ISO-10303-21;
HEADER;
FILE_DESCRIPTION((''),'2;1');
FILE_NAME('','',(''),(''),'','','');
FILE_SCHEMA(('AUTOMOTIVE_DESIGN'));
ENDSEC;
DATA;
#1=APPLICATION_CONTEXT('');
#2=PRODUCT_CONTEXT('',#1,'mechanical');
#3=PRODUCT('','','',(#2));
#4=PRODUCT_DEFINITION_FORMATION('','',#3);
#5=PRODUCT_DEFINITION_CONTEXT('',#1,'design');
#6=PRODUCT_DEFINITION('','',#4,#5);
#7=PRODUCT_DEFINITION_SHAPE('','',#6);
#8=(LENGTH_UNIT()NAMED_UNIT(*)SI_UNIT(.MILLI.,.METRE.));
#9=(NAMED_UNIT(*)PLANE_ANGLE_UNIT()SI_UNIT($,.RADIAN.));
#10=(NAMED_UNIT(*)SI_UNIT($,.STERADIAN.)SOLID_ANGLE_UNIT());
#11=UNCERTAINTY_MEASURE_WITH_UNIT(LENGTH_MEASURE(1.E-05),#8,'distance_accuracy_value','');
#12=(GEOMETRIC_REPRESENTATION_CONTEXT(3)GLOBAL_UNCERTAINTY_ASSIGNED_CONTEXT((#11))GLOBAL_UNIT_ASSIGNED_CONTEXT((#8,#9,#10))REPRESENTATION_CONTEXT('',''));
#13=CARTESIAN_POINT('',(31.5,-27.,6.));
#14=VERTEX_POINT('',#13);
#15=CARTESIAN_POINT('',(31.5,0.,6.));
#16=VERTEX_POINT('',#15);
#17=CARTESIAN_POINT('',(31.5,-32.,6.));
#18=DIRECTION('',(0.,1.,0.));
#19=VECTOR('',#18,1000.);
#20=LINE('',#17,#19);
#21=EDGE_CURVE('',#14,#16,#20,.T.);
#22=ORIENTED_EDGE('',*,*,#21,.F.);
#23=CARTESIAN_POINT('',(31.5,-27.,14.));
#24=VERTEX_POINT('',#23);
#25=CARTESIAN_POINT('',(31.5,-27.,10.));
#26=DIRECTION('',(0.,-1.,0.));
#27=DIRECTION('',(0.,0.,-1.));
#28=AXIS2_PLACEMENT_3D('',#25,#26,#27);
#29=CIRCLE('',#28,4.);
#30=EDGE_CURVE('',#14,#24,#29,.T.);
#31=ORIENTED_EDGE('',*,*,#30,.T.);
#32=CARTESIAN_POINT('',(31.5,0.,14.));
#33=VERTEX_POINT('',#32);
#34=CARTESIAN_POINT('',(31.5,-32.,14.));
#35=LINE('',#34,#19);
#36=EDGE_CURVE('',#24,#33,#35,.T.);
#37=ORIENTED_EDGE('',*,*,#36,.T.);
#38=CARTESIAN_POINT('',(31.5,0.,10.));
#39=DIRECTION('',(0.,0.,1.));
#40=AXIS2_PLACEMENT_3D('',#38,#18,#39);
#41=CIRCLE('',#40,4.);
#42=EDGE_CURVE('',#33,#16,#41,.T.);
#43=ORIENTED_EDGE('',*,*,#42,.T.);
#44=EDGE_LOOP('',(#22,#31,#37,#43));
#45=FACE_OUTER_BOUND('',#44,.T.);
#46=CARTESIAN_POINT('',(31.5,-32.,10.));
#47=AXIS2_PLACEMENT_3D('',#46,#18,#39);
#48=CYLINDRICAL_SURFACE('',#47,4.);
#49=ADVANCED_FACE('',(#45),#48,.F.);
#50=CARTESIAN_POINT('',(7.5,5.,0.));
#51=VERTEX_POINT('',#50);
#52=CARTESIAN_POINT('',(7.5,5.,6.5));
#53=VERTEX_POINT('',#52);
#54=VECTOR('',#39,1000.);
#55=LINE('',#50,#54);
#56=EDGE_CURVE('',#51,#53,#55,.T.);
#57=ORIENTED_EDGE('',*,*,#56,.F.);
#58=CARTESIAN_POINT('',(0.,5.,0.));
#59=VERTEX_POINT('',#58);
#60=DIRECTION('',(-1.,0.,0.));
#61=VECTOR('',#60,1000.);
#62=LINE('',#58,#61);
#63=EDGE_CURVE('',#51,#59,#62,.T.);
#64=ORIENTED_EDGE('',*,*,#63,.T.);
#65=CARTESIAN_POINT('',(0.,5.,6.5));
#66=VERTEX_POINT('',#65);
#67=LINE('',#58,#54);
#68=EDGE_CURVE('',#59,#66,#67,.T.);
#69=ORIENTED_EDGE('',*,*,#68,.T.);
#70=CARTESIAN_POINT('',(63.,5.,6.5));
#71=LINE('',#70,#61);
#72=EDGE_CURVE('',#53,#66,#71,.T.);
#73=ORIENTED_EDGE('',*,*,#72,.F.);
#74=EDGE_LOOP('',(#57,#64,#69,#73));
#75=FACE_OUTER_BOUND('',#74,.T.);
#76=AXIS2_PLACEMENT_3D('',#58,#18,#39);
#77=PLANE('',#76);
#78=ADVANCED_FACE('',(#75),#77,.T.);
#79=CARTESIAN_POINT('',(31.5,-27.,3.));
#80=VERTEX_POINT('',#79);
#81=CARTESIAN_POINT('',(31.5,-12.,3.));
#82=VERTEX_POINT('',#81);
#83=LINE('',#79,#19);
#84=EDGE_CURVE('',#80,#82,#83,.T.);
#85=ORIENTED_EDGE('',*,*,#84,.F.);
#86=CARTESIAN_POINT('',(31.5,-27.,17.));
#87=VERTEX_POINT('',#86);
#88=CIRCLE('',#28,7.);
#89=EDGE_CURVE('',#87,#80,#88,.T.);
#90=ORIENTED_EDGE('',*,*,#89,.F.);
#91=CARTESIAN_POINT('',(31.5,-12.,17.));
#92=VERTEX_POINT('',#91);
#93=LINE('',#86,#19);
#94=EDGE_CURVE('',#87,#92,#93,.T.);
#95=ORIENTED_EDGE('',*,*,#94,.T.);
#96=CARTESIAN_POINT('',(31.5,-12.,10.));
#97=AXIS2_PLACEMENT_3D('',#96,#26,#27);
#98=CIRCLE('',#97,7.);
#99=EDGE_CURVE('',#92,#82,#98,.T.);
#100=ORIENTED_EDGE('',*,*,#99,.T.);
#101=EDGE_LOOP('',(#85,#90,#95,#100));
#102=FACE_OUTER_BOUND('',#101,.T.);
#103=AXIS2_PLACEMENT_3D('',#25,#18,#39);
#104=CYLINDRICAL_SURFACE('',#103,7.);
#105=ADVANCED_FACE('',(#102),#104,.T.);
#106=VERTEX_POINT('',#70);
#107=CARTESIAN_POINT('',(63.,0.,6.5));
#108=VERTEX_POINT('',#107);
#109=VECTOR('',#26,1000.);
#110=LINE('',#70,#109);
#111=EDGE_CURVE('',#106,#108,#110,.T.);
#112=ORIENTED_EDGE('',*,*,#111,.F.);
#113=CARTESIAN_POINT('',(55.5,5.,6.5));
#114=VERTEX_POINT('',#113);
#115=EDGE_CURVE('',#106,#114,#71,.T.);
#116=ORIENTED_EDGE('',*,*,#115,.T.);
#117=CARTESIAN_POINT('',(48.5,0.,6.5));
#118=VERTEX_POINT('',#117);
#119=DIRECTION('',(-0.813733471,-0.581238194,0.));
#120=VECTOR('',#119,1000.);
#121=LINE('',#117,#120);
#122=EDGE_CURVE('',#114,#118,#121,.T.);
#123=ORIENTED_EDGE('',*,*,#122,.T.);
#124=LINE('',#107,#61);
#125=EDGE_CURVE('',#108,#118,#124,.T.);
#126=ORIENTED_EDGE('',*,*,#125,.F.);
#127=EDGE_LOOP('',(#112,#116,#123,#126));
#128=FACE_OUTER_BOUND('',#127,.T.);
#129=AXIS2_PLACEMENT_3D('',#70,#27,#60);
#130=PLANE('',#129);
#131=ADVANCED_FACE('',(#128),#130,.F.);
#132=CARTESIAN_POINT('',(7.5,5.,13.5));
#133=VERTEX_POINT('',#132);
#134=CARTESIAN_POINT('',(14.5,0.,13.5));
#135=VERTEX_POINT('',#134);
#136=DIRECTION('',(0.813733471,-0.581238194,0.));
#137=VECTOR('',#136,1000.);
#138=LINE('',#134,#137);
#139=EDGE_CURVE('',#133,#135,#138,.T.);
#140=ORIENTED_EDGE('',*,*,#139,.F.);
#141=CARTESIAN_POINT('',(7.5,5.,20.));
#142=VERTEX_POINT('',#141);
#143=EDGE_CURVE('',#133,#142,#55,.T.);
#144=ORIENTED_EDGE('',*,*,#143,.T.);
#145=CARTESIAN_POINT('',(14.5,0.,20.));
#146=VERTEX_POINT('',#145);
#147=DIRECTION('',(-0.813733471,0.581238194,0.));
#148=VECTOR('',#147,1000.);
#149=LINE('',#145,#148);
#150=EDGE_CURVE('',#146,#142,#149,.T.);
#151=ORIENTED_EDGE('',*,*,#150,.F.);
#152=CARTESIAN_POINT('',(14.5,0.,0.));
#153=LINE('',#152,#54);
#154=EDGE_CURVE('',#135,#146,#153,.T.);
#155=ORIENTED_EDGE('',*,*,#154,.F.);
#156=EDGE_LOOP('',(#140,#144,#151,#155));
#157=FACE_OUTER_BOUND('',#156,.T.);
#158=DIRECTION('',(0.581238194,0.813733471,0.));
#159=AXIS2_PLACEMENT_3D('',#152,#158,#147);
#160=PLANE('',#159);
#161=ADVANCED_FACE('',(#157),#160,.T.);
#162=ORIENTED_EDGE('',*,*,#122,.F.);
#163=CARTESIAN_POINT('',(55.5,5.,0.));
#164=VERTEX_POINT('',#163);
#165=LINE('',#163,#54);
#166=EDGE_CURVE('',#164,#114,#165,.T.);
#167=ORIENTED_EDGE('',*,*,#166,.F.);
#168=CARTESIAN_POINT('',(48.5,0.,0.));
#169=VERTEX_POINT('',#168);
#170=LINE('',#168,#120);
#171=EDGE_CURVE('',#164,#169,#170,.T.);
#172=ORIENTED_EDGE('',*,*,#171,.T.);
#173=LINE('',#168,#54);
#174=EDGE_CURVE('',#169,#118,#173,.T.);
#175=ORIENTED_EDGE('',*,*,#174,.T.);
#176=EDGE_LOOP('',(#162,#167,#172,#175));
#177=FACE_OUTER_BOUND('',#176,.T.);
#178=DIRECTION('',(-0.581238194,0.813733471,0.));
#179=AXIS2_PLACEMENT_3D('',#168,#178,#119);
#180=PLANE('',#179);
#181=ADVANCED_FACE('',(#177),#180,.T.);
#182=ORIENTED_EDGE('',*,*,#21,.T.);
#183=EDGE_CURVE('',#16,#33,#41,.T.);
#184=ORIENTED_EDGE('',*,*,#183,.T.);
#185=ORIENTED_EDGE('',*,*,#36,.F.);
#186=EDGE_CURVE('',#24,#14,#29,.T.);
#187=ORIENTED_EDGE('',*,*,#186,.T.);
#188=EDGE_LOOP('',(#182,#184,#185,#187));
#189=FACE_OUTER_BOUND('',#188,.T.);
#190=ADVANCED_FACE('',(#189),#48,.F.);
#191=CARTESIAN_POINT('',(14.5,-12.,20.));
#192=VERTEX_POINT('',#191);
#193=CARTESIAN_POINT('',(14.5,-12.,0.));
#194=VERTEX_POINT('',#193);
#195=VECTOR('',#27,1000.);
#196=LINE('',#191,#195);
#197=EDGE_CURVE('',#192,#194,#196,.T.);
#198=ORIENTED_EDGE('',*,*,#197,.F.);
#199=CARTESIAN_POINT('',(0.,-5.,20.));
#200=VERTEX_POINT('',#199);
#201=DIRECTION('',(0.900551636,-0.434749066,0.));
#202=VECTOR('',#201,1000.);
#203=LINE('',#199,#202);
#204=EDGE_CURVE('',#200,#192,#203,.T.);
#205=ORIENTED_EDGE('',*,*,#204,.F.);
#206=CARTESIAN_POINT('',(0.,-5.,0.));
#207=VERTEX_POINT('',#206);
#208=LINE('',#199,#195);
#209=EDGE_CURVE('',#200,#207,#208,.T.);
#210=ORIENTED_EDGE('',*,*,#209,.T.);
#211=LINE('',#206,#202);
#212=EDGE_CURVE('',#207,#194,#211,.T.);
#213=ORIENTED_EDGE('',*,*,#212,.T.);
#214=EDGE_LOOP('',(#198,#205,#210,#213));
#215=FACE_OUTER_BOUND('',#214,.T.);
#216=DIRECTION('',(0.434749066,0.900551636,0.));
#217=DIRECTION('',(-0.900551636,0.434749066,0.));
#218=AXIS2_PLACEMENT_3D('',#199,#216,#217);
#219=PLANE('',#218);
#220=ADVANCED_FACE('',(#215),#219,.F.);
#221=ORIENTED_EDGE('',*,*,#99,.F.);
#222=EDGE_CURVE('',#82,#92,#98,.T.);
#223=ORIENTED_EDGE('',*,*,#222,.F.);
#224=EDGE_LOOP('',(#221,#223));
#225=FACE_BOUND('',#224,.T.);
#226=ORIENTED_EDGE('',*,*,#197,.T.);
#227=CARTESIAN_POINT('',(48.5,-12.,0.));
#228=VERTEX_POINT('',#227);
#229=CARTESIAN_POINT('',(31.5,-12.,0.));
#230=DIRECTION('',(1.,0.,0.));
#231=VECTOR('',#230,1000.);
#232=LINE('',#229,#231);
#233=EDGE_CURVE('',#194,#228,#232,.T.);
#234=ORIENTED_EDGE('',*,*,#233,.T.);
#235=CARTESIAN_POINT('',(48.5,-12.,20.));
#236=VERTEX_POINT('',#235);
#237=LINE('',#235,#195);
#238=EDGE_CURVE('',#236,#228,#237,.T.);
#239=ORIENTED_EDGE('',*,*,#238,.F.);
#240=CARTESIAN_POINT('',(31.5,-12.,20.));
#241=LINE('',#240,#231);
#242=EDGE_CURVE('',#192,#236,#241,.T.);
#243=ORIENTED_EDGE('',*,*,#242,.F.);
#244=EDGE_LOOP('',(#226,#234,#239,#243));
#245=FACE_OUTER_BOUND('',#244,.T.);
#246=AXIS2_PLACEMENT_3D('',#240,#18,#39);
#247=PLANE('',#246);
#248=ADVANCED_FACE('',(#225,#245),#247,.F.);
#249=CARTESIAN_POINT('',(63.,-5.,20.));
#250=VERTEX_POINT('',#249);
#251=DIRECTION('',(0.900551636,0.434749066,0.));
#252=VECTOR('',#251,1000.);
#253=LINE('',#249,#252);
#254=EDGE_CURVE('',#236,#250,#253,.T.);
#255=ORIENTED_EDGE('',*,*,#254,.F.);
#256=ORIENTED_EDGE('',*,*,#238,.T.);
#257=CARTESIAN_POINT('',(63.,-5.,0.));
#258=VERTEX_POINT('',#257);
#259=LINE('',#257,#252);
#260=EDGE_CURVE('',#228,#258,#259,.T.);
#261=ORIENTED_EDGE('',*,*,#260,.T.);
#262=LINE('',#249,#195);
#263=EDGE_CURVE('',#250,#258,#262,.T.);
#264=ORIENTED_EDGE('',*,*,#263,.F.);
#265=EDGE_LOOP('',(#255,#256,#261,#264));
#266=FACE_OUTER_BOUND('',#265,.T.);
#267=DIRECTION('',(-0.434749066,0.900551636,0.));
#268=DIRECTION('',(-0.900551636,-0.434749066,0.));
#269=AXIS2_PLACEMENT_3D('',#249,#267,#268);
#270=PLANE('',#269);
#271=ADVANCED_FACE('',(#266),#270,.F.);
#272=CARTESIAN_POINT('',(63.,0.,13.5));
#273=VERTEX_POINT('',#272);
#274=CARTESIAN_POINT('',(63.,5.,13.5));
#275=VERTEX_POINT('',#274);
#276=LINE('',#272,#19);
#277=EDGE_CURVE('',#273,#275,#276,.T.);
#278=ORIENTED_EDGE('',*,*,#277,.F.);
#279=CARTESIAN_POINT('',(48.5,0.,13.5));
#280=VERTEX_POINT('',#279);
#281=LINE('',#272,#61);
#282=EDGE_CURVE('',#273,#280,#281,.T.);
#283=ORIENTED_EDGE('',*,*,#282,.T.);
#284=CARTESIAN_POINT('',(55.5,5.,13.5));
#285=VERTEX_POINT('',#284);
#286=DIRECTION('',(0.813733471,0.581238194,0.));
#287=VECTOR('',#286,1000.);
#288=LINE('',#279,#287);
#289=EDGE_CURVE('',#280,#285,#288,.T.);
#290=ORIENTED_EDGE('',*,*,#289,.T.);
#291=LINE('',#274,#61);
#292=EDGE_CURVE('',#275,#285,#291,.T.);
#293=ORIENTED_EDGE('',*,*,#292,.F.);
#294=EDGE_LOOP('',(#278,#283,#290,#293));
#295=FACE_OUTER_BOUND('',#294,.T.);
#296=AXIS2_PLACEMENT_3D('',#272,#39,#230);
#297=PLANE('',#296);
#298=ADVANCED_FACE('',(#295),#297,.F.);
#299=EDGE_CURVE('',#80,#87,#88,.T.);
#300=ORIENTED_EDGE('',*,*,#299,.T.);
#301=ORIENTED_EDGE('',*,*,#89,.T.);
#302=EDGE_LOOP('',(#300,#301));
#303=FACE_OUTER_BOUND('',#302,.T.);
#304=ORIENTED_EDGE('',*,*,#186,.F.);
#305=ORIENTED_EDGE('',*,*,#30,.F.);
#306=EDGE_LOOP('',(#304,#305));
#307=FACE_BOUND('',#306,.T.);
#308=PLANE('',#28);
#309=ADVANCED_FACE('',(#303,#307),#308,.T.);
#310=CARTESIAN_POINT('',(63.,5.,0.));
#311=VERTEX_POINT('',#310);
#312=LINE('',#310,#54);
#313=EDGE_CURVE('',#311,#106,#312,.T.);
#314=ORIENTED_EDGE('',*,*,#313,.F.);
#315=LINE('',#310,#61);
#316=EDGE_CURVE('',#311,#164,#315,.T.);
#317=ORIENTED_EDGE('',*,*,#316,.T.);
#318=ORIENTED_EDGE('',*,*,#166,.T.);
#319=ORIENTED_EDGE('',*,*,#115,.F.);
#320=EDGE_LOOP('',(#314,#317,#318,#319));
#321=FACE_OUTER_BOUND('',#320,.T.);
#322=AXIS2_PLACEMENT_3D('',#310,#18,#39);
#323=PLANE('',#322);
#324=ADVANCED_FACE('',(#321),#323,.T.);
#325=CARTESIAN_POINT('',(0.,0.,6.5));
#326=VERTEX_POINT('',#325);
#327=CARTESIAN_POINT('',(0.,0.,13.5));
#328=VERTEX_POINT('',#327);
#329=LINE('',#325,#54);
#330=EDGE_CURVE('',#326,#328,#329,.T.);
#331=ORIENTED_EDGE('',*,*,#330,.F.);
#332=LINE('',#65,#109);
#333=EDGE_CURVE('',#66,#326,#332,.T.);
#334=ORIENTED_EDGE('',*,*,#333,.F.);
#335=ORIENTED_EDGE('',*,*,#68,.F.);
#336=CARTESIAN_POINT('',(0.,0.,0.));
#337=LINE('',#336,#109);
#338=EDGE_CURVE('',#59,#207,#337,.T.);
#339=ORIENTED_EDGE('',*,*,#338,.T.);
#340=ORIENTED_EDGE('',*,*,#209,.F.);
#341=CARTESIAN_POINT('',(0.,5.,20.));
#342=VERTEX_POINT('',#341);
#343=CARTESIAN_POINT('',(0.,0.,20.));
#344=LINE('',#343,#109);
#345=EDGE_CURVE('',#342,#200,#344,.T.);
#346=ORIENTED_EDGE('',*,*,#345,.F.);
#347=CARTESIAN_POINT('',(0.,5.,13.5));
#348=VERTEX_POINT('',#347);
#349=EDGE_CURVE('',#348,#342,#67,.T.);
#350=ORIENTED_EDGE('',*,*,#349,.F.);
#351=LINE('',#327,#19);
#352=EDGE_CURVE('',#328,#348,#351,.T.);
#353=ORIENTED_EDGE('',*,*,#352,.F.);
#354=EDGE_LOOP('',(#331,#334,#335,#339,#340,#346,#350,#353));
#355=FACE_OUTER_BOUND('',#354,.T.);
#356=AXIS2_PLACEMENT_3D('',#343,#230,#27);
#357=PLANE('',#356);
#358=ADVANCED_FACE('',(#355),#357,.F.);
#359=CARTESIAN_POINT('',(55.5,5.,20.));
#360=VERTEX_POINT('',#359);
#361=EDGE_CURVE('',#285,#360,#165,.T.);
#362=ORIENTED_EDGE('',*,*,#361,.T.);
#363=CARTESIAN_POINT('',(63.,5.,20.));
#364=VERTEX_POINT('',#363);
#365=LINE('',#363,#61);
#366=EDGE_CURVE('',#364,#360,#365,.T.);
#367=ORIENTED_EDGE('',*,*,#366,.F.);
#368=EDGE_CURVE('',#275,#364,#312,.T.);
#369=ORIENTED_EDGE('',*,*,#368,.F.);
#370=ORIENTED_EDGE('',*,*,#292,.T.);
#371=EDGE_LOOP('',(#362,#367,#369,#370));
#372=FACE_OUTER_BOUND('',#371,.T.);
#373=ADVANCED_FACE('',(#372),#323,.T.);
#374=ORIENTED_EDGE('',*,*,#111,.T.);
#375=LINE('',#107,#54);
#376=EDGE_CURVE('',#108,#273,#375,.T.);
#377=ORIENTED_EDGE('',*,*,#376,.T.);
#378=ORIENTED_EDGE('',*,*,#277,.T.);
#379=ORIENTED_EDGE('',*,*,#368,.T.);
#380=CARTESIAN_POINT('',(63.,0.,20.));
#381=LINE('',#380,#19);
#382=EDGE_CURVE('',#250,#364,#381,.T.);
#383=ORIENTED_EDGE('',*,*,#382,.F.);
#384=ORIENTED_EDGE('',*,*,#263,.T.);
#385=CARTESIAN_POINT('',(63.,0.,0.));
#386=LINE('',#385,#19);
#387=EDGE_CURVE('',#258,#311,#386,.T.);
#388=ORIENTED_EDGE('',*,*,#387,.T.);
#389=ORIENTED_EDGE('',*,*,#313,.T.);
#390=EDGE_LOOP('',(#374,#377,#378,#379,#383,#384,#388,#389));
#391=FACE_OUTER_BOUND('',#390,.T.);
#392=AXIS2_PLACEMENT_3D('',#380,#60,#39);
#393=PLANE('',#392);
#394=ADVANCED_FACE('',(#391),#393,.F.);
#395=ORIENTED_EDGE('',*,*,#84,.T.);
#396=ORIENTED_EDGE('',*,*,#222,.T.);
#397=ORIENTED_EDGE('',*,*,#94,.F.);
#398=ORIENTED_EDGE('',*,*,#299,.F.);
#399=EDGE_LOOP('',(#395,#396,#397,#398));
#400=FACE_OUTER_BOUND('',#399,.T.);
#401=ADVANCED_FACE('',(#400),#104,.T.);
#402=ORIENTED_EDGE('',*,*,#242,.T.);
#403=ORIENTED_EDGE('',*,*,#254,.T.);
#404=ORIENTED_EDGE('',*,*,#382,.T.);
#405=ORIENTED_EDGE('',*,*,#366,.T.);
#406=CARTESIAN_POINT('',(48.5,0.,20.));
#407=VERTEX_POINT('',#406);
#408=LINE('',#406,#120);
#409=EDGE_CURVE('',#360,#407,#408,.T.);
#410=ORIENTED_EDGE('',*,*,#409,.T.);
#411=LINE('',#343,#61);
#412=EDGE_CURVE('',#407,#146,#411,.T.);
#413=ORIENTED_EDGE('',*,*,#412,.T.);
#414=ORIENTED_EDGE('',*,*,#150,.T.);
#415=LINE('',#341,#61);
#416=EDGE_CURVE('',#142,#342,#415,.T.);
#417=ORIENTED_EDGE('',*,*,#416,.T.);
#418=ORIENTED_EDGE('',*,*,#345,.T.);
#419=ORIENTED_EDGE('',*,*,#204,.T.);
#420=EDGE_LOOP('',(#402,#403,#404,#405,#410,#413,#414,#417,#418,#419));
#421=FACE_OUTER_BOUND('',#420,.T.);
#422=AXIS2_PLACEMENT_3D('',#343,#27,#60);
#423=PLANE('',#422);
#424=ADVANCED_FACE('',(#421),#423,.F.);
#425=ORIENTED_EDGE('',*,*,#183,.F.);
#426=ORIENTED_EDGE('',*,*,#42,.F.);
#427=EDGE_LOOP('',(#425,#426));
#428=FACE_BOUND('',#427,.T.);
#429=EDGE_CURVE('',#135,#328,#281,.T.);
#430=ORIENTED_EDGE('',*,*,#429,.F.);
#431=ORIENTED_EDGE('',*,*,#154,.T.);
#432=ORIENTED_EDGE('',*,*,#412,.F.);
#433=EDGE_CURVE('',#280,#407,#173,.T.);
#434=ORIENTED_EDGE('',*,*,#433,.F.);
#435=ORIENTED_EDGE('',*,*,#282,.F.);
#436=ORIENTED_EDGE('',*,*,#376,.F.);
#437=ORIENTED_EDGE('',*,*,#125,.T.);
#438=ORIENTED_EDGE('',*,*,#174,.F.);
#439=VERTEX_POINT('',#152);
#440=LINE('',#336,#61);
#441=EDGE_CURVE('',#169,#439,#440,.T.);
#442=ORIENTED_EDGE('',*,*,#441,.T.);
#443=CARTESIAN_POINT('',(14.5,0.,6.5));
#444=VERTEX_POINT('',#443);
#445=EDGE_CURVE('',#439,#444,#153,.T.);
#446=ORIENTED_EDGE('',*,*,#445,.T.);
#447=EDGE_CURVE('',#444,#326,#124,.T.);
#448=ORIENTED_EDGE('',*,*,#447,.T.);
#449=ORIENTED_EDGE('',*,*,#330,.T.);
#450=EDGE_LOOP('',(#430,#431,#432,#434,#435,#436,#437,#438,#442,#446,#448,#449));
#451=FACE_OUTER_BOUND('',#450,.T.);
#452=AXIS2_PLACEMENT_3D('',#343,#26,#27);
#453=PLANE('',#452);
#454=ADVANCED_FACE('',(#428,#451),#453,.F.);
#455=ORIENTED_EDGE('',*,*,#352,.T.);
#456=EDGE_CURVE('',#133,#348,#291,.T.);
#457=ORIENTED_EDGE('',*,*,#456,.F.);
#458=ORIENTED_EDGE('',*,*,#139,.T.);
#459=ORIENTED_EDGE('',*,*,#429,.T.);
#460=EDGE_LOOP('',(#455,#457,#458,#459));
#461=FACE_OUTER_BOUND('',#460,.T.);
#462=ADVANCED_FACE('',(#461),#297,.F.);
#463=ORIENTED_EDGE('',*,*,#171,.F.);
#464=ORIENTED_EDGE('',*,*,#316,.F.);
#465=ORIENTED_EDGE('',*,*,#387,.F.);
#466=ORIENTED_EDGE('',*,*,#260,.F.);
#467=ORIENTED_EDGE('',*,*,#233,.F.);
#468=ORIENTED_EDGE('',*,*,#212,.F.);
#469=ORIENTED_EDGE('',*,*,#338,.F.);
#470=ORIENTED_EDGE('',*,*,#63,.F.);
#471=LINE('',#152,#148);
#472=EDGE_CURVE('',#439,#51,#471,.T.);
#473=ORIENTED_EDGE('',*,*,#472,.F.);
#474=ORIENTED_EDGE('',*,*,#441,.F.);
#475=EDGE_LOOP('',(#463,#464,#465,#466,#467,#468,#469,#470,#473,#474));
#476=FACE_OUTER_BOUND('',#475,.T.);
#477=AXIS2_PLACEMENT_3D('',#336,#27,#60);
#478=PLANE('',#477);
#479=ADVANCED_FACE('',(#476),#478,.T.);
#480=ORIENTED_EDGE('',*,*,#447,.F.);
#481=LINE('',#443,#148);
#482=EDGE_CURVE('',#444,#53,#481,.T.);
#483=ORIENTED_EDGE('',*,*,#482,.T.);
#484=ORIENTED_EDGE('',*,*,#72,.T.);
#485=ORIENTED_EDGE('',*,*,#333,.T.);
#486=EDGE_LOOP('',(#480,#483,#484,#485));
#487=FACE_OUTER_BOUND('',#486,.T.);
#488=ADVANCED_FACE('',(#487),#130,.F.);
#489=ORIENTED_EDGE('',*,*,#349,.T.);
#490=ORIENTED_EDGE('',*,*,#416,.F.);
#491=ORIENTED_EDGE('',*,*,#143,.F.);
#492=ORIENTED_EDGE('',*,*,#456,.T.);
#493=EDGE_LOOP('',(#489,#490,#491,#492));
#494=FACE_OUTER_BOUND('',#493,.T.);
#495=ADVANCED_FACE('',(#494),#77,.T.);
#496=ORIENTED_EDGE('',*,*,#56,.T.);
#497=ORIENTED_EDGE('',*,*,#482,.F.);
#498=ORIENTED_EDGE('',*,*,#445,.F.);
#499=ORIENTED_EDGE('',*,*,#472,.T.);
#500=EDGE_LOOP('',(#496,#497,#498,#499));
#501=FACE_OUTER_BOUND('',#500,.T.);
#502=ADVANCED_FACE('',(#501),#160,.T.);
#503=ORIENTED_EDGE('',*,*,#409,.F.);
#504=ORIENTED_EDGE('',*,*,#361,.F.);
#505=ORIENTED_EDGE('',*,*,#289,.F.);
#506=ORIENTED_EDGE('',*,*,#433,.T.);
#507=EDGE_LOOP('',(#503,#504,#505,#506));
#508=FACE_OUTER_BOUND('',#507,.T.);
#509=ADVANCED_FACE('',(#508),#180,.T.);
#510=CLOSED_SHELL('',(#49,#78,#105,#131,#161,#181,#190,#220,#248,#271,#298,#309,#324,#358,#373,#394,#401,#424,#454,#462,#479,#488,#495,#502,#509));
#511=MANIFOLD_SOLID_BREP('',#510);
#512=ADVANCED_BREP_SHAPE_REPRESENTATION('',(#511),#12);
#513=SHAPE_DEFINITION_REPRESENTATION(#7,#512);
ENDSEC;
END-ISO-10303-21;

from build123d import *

# Parameters (mm, degrees)
BASE_BLOCK_DEPTH         = 20
END_LUGS_DEPTH           = 20
GUIDE_V_SLOT_DEPTH       = 63
LOCATING_PIN_SKETCH_14_R = 7
LOCATING_PIN_14_DEPTH    = 15
HOLE_SKETCH_8_R          = 4
HOLE_8_DEPTH             = 32


with BuildPart() as part:
    # Base Profile Sketch → Base Block (new body)
    with BuildSketch(Plane.XY):
        Polygon((0, 0), (63, 0), (63, -5), (48.5, -12), (31.5, -12), (14.5, -12), (0, -5), align=None)
    extrude(amount=BASE_BLOCK_DEPTH)

    # End Lugs Sketch → End Lugs (add)
    with BuildSketch(Plane.XY.offset(20)):
        Polygon((0, 0), (0, 5), (7.5, 5), (14.5, 0), align=None)
        Polygon((63, 0), (63, 5), (55.5, 5), (48.5, 0), align=None)
    extrude(amount=-END_LUGS_DEPTH)

    # Guide V-Slot Sketch → Guide V-Slot (cut)
    with BuildSketch(Plane.ZY):
        Polygon((10, 5), (6.5, 5), (6.5, 0), (13.5, 0), (13.5, 5), align=None)
    extrude(amount=-GUIDE_V_SLOT_DEPTH, mode=Mode.SUBTRACT)

    # Locating Pin Sketch Ø14 → Locating Pin Ø14 (add)
    with BuildSketch(Plane.XZ.offset(12)):
        with Locations(Location((31.5, 10, 0), (0, 0, 270))):
            Circle(LOCATING_PIN_SKETCH_14_R)
    extrude(amount=LOCATING_PIN_14_DEPTH)

    # Hole Sketch Ø8 → Hole Ø8 (cut)
    with BuildSketch(Plane(origin=(0, 0, 0), x_dir=(1, 0, 0), z_dir=(0, 1, 0))):
        with Locations(Location((31.5, -10, 0), (0, 0, 270))):
            Circle(HOLE_SKETCH_8_R)
    extrude(amount=-HOLE_8_DEPTH, mode=Mode.SUBTRACT)


solid = part.part
